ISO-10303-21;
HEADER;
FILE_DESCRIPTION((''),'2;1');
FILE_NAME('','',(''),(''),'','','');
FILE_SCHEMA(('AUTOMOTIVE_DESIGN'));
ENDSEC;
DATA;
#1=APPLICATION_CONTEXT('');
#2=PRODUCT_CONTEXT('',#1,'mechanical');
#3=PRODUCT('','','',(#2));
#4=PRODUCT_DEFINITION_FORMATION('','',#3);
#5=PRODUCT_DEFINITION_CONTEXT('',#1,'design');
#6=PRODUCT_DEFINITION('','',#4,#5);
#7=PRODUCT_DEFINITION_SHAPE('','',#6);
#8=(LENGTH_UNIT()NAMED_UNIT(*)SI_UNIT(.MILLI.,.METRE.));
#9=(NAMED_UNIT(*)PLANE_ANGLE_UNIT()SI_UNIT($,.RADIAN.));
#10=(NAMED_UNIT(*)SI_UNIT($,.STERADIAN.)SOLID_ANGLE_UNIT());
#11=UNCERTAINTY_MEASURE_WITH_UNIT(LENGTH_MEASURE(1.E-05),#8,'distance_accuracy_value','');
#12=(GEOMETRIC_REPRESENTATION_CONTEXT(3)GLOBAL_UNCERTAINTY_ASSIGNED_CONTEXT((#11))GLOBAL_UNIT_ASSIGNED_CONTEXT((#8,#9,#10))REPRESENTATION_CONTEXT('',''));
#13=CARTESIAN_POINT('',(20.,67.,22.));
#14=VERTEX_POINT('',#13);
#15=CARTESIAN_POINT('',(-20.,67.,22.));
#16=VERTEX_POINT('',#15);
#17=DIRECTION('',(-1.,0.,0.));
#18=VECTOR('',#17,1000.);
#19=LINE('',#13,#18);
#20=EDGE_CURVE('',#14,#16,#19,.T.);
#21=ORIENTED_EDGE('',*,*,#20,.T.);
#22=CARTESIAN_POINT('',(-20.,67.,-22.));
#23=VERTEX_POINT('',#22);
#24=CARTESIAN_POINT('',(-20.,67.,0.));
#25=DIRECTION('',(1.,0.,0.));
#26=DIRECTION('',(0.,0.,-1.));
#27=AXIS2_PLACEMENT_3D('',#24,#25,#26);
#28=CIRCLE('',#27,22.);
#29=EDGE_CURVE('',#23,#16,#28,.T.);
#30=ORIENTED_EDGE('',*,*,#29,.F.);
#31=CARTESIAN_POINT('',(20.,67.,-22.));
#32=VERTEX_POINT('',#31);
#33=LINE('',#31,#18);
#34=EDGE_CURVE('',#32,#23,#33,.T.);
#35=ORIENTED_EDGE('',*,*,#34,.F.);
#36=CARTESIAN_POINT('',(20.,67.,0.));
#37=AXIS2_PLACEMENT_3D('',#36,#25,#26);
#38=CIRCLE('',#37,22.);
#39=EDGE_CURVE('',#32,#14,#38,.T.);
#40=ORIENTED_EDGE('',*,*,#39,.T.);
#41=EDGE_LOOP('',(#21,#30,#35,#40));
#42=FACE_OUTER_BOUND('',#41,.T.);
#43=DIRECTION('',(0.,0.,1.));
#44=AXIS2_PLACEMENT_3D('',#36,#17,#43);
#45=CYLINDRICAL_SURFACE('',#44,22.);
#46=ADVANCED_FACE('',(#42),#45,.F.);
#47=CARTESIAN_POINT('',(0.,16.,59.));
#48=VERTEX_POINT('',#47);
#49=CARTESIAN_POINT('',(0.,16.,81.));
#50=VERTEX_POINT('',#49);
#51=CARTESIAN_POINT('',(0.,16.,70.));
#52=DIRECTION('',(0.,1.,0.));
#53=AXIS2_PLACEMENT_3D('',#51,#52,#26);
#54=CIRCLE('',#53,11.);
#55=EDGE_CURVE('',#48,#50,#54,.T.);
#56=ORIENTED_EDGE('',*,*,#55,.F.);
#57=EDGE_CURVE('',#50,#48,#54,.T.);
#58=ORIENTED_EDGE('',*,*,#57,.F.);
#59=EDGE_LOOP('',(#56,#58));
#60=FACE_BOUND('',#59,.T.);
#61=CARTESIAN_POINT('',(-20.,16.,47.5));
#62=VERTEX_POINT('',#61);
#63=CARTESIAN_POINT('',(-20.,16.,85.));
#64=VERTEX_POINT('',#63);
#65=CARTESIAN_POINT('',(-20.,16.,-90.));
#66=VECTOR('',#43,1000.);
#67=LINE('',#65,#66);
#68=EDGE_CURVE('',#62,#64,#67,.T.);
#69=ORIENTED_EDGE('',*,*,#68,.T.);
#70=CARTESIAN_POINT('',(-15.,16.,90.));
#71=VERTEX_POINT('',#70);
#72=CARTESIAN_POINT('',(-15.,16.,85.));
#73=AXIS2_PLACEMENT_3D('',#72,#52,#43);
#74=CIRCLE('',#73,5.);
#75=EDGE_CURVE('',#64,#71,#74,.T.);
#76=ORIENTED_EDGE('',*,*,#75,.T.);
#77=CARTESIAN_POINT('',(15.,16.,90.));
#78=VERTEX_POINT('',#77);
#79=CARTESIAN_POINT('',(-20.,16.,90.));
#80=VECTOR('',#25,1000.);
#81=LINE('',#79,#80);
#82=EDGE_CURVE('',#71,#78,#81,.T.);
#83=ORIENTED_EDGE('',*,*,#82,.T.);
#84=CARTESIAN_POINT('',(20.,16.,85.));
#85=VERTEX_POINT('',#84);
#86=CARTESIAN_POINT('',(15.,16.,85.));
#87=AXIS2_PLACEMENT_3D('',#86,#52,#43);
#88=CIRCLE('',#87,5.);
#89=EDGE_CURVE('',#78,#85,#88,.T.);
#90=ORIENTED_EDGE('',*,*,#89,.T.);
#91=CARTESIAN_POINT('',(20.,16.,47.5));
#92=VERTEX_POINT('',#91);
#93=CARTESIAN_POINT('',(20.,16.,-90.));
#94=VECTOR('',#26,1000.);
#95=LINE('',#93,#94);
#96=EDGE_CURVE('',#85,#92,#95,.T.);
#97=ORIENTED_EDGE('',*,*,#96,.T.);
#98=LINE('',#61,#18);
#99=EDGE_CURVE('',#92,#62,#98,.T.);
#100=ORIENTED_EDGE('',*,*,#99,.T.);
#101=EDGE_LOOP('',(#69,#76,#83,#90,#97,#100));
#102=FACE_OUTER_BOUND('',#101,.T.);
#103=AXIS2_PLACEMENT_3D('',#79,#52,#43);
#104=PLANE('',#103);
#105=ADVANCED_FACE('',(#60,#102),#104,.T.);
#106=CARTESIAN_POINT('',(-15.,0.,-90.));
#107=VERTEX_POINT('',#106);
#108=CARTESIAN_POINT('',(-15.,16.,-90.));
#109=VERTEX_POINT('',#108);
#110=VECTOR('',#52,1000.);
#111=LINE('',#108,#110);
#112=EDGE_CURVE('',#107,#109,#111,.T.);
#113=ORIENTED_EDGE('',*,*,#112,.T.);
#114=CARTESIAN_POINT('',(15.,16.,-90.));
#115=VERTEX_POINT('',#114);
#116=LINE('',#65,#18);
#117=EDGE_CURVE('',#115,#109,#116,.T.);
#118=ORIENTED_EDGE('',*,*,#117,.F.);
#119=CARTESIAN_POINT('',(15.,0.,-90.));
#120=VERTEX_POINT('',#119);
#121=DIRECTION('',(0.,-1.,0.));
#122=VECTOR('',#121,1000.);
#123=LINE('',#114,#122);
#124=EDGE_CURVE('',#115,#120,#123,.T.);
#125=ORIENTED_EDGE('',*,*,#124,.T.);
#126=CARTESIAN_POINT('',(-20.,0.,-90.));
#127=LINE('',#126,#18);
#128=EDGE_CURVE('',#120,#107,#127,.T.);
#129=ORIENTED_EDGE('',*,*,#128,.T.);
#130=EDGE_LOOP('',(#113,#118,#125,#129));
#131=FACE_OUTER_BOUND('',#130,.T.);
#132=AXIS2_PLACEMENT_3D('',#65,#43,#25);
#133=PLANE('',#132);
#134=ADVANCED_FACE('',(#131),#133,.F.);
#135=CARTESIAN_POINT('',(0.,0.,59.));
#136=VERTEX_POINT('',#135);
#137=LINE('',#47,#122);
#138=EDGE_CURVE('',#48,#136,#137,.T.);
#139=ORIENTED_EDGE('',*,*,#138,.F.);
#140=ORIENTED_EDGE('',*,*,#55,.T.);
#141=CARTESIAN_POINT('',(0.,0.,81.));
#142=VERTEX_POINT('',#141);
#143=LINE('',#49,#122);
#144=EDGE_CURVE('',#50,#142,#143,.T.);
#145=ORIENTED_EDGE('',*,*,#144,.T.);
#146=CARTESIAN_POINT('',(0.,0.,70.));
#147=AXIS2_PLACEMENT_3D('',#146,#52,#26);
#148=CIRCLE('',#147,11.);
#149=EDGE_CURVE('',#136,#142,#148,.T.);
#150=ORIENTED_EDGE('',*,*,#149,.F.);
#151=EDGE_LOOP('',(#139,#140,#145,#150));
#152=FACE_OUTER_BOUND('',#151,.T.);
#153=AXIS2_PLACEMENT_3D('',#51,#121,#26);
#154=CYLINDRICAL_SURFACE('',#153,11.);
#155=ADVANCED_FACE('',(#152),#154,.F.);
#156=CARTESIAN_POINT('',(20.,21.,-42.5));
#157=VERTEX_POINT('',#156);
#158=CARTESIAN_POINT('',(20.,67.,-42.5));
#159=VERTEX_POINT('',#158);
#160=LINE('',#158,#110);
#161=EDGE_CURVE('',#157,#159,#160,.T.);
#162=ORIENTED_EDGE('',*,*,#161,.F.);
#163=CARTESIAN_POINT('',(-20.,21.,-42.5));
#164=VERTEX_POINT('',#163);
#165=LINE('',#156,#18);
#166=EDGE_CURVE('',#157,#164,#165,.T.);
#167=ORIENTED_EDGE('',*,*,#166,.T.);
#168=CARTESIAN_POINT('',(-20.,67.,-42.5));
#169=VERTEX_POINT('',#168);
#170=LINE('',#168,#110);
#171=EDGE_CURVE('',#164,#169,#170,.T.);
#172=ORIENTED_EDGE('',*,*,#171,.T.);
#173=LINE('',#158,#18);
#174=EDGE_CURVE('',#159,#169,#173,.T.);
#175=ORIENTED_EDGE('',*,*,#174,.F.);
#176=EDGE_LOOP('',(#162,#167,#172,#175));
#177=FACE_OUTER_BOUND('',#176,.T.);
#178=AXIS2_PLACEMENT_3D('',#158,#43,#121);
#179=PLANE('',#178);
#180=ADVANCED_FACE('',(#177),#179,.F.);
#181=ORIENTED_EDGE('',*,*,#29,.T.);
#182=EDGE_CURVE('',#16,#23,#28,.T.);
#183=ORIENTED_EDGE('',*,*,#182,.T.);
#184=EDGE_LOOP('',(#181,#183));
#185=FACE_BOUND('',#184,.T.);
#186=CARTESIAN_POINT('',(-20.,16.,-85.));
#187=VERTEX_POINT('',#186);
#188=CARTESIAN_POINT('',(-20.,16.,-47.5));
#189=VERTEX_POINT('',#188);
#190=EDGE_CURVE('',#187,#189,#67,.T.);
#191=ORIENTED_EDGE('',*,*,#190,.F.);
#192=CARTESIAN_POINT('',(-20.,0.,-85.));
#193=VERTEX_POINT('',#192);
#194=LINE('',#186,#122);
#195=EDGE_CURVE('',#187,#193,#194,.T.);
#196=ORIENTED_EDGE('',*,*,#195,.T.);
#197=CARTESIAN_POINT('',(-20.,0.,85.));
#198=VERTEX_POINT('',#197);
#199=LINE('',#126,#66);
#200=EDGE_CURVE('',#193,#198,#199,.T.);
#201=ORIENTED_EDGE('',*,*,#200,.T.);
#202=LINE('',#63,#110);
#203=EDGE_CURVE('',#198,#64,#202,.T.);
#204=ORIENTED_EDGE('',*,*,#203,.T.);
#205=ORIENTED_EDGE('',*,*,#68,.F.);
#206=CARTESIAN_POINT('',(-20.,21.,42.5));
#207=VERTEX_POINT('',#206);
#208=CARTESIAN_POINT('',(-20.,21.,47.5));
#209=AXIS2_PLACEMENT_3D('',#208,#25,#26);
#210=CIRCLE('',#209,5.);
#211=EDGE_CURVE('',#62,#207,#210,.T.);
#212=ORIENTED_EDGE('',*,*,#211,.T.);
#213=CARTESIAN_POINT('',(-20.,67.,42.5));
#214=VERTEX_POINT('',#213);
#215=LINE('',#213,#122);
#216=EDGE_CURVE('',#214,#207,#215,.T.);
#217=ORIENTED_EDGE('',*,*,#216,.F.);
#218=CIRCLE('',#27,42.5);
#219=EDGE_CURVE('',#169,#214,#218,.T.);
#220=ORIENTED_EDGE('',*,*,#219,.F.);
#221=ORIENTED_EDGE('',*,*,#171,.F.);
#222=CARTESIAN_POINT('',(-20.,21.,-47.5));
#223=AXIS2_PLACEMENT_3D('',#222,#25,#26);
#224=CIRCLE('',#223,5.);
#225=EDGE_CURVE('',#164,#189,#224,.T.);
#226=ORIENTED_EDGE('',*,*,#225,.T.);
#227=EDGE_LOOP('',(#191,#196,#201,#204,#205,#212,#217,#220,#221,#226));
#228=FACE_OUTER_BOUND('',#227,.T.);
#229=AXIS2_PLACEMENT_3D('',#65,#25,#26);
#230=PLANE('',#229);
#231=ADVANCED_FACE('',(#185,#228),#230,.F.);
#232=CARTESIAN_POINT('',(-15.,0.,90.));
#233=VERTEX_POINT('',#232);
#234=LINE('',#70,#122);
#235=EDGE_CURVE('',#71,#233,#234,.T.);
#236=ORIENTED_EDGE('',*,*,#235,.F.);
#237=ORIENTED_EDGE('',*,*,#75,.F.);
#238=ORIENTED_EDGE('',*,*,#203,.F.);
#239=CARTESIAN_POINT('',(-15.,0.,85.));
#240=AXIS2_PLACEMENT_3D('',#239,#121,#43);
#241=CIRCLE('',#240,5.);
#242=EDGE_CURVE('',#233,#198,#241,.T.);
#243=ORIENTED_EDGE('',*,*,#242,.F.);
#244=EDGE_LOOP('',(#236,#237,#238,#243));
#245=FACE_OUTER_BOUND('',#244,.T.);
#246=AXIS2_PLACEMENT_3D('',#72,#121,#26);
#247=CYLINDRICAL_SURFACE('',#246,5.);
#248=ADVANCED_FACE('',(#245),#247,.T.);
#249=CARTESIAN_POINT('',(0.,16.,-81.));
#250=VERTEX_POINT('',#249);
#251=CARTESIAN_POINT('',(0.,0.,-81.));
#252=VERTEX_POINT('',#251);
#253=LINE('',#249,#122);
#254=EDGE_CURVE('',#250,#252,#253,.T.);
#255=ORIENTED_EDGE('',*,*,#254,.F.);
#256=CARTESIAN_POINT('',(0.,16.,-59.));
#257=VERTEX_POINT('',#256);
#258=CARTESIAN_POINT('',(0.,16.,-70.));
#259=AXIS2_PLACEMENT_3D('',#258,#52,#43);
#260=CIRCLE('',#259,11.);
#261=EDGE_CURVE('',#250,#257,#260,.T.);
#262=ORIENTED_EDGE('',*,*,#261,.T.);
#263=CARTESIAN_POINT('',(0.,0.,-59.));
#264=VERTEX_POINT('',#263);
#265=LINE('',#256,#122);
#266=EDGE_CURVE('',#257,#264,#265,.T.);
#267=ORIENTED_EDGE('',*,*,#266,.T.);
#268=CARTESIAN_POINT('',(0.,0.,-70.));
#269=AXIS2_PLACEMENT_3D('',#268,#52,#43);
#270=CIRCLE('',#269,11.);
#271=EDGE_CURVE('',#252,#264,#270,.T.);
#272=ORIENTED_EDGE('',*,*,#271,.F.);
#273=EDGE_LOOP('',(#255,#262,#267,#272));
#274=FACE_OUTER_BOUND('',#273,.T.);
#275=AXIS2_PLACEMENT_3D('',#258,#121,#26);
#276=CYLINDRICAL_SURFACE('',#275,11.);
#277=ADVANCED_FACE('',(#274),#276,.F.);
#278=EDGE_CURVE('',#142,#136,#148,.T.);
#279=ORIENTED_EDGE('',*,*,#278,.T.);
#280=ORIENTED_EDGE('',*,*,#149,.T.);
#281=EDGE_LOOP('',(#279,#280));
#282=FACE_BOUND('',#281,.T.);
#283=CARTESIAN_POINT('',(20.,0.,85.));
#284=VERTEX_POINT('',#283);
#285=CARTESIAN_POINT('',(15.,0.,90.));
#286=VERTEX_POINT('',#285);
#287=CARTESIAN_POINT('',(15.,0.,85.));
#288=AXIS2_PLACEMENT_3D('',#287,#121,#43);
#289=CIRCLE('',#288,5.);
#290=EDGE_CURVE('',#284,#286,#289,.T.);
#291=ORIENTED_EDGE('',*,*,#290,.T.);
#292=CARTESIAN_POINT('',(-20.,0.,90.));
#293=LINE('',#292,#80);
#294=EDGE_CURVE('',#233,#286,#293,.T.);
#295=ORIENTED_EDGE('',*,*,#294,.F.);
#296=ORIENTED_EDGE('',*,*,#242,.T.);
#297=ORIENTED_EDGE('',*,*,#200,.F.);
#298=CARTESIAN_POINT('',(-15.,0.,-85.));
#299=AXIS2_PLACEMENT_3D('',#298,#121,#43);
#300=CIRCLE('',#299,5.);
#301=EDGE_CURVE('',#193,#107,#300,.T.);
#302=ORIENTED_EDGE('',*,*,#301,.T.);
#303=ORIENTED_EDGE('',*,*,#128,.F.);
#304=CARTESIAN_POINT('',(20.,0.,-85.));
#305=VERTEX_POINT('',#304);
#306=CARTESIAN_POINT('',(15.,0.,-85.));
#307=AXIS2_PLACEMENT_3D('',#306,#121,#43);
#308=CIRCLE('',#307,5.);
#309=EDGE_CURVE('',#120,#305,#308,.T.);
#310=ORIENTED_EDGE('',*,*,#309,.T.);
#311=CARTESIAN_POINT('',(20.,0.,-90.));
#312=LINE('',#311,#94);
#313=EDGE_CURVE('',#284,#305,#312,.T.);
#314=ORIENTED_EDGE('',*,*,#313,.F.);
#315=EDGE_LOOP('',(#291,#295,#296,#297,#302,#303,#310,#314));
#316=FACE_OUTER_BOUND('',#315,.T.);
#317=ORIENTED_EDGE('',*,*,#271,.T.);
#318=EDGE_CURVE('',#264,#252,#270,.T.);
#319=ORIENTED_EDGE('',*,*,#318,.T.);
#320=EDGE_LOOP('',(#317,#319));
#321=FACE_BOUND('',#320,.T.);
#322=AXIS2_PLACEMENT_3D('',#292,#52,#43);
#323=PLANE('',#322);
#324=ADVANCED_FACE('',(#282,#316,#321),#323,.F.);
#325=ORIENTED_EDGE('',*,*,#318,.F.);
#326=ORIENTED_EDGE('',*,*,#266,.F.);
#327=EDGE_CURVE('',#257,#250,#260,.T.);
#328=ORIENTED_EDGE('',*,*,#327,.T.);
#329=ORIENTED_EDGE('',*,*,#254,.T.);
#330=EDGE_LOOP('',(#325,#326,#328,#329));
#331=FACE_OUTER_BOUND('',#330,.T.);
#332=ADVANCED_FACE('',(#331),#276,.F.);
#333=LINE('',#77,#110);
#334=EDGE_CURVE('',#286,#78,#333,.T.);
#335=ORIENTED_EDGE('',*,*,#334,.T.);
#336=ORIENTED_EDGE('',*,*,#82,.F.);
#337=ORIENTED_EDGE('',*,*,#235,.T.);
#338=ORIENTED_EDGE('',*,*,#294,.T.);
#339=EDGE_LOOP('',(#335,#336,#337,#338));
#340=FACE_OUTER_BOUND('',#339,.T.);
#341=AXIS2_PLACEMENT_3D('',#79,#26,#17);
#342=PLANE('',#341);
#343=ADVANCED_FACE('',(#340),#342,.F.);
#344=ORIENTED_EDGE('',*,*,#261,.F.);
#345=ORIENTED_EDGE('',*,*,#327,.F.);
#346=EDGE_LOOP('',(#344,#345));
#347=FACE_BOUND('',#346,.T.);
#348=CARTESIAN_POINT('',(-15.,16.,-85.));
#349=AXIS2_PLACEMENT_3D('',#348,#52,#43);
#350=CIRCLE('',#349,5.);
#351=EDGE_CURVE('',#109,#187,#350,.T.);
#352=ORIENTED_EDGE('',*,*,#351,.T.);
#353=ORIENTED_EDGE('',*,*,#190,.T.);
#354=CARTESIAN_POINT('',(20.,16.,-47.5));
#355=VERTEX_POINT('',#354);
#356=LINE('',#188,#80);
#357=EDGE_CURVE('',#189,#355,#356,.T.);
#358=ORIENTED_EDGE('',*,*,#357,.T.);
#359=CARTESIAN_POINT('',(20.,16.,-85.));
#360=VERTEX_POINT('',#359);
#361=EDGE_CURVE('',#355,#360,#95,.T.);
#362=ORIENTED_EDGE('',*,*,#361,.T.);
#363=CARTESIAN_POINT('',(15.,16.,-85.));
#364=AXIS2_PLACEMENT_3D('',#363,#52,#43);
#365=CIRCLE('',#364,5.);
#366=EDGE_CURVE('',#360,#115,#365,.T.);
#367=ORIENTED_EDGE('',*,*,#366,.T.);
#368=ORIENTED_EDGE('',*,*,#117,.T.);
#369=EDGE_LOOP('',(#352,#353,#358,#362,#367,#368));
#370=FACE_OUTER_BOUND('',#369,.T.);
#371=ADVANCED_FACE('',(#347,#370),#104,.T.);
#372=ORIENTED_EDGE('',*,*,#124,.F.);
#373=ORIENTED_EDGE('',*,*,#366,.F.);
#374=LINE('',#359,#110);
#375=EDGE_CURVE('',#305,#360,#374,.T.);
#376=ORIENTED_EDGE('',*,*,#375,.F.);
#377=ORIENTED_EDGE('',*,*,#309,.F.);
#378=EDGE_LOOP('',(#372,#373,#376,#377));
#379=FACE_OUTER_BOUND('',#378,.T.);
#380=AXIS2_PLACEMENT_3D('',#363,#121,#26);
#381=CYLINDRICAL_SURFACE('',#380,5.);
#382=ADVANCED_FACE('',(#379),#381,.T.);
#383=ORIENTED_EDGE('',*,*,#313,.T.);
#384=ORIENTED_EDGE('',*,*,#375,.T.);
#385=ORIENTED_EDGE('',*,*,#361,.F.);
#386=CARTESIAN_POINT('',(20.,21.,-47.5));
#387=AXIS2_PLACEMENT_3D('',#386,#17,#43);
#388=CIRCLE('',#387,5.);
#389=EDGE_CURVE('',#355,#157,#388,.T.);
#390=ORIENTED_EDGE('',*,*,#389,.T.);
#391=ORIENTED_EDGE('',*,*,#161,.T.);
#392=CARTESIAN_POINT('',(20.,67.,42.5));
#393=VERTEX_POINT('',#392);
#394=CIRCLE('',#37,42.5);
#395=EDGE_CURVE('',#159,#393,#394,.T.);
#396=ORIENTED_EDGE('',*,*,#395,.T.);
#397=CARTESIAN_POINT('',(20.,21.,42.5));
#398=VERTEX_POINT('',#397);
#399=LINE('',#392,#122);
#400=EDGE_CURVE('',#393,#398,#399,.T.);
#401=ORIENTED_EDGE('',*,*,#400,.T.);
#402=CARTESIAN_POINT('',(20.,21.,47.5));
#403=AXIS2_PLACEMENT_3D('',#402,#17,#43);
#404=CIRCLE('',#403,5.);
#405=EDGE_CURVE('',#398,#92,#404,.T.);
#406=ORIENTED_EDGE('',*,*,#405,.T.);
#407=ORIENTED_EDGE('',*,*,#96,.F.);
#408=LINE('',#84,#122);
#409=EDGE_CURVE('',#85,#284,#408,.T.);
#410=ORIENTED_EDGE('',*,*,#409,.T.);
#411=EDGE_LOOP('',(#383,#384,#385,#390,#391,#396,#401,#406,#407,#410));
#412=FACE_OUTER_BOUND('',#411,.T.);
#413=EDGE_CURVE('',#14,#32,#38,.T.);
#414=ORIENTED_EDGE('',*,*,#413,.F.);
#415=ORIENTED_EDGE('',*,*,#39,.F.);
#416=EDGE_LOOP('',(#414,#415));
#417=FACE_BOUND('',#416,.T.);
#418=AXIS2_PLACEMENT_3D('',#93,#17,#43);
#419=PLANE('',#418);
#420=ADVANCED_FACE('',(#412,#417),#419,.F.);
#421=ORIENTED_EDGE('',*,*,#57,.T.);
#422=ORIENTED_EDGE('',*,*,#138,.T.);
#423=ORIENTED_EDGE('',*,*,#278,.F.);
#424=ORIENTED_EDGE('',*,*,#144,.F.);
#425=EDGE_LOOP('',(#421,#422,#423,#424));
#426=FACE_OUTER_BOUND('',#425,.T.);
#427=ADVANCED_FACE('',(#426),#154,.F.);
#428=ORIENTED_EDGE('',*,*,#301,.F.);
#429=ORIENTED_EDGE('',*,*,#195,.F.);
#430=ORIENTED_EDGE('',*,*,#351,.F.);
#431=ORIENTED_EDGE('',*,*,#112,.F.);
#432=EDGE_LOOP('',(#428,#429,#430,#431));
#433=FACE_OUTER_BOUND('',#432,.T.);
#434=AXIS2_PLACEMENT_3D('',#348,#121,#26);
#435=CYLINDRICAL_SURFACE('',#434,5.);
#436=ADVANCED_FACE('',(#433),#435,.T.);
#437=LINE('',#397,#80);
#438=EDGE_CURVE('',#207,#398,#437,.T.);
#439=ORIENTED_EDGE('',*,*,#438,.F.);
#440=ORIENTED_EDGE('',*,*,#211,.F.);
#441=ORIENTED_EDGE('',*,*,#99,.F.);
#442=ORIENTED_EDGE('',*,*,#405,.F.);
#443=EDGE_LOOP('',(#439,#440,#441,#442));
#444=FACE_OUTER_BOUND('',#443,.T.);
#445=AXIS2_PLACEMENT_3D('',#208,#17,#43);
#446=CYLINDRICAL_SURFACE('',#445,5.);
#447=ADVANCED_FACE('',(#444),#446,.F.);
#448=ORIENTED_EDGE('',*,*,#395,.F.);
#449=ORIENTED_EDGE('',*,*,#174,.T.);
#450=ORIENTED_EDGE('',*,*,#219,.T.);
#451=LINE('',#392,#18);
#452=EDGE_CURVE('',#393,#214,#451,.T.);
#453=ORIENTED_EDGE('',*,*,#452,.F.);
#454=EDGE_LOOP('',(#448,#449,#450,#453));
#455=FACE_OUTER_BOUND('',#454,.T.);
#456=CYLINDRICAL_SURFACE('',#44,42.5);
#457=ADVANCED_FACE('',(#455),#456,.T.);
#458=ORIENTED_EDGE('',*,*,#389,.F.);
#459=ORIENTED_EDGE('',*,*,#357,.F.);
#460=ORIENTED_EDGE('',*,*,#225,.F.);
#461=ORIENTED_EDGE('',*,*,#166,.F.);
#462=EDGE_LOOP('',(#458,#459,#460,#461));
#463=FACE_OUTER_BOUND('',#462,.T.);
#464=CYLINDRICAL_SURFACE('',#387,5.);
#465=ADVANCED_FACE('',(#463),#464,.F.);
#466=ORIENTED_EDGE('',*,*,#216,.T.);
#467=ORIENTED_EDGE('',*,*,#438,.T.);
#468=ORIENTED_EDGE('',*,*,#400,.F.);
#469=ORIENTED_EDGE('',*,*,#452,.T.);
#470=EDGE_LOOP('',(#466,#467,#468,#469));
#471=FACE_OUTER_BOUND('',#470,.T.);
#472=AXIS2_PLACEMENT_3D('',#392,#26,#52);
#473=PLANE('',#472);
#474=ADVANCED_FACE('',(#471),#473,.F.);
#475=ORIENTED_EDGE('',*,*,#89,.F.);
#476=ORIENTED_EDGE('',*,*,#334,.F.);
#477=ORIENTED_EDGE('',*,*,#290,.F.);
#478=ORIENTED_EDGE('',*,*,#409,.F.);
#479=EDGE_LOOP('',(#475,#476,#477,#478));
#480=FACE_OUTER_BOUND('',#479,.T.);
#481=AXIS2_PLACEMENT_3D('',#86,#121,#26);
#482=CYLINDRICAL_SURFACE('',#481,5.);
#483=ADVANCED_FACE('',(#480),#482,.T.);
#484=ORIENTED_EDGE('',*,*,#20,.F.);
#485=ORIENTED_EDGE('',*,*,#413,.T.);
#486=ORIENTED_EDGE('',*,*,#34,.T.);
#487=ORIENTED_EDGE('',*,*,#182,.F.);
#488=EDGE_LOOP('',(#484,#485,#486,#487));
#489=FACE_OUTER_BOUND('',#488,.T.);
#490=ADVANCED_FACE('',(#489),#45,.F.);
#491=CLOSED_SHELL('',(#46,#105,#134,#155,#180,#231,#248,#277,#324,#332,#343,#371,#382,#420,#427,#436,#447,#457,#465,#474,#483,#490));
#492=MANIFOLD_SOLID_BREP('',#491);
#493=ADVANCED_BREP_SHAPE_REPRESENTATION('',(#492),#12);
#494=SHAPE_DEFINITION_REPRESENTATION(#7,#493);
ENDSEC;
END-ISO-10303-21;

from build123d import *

# Parameters (mm, degrees)
SKETCH1_W           = 40
SKETCH1_H           = 180
SKETCH1_R           = 11
BOSS_EXTRUDE1_DEPTH = 16
SKETCH2_R           = 22
BOSS_EXTRUDE2_DEPTH = 20
FILLET1_R           = 5


with BuildPart() as part:
    # Sketch1 → Boss-Extrude1 (new body)
    with BuildSketch(Plane(origin=(0, 0, 0), x_dir=(1, 0, 0), z_dir=(0, 1, 0))):
        Rectangle(SKETCH1_W, SKETCH1_H)
        with Locations(Location((0, 70, 0), (0, 0, 270))):
            Circle(SKETCH1_R, mode=Mode.SUBTRACT)
        with Locations(Location((0, -70, 0), (0, 0, 90))):
            Circle(SKETCH1_R, mode=Mode.SUBTRACT)
    extrude(amount=BOSS_EXTRUDE1_DEPTH)

    # Sketch2 → Boss-Extrude2 (add, symmetric)
    with BuildSketch(Plane(origin=(0, 0, 0), x_dir=(0, 0, -1), z_dir=(1, 0, 0))):
        with BuildLine():
            Line((-42.5, 67), (-42.5, 16))
            Line((-42.5, 16), (42.5, 16))
            Line((42.5, 16), (42.5, 67))
            ThreePointArc((42.5, 67), (0, 109.5), (-42.5, 67))
        make_face()
        with Locations((0, 67)):
            Circle(SKETCH2_R, mode=Mode.SUBTRACT)
    extrude(amount=BOSS_EXTRUDE2_DEPTH, both=True)

    # Fillet1
    fillet1_edges = [part.edges().sort_by_distance(p)[0] for p in [
        (0, 16, 42.5),
        (20, 8, 90),
        (-20, 8, 90),
        (20, 8, -90),
        (-20, 8, -90),
        (0, 16, -42.5),
    ]]
    fillet(fillet1_edges, radius=FILLET1_R)


solid = part.part
